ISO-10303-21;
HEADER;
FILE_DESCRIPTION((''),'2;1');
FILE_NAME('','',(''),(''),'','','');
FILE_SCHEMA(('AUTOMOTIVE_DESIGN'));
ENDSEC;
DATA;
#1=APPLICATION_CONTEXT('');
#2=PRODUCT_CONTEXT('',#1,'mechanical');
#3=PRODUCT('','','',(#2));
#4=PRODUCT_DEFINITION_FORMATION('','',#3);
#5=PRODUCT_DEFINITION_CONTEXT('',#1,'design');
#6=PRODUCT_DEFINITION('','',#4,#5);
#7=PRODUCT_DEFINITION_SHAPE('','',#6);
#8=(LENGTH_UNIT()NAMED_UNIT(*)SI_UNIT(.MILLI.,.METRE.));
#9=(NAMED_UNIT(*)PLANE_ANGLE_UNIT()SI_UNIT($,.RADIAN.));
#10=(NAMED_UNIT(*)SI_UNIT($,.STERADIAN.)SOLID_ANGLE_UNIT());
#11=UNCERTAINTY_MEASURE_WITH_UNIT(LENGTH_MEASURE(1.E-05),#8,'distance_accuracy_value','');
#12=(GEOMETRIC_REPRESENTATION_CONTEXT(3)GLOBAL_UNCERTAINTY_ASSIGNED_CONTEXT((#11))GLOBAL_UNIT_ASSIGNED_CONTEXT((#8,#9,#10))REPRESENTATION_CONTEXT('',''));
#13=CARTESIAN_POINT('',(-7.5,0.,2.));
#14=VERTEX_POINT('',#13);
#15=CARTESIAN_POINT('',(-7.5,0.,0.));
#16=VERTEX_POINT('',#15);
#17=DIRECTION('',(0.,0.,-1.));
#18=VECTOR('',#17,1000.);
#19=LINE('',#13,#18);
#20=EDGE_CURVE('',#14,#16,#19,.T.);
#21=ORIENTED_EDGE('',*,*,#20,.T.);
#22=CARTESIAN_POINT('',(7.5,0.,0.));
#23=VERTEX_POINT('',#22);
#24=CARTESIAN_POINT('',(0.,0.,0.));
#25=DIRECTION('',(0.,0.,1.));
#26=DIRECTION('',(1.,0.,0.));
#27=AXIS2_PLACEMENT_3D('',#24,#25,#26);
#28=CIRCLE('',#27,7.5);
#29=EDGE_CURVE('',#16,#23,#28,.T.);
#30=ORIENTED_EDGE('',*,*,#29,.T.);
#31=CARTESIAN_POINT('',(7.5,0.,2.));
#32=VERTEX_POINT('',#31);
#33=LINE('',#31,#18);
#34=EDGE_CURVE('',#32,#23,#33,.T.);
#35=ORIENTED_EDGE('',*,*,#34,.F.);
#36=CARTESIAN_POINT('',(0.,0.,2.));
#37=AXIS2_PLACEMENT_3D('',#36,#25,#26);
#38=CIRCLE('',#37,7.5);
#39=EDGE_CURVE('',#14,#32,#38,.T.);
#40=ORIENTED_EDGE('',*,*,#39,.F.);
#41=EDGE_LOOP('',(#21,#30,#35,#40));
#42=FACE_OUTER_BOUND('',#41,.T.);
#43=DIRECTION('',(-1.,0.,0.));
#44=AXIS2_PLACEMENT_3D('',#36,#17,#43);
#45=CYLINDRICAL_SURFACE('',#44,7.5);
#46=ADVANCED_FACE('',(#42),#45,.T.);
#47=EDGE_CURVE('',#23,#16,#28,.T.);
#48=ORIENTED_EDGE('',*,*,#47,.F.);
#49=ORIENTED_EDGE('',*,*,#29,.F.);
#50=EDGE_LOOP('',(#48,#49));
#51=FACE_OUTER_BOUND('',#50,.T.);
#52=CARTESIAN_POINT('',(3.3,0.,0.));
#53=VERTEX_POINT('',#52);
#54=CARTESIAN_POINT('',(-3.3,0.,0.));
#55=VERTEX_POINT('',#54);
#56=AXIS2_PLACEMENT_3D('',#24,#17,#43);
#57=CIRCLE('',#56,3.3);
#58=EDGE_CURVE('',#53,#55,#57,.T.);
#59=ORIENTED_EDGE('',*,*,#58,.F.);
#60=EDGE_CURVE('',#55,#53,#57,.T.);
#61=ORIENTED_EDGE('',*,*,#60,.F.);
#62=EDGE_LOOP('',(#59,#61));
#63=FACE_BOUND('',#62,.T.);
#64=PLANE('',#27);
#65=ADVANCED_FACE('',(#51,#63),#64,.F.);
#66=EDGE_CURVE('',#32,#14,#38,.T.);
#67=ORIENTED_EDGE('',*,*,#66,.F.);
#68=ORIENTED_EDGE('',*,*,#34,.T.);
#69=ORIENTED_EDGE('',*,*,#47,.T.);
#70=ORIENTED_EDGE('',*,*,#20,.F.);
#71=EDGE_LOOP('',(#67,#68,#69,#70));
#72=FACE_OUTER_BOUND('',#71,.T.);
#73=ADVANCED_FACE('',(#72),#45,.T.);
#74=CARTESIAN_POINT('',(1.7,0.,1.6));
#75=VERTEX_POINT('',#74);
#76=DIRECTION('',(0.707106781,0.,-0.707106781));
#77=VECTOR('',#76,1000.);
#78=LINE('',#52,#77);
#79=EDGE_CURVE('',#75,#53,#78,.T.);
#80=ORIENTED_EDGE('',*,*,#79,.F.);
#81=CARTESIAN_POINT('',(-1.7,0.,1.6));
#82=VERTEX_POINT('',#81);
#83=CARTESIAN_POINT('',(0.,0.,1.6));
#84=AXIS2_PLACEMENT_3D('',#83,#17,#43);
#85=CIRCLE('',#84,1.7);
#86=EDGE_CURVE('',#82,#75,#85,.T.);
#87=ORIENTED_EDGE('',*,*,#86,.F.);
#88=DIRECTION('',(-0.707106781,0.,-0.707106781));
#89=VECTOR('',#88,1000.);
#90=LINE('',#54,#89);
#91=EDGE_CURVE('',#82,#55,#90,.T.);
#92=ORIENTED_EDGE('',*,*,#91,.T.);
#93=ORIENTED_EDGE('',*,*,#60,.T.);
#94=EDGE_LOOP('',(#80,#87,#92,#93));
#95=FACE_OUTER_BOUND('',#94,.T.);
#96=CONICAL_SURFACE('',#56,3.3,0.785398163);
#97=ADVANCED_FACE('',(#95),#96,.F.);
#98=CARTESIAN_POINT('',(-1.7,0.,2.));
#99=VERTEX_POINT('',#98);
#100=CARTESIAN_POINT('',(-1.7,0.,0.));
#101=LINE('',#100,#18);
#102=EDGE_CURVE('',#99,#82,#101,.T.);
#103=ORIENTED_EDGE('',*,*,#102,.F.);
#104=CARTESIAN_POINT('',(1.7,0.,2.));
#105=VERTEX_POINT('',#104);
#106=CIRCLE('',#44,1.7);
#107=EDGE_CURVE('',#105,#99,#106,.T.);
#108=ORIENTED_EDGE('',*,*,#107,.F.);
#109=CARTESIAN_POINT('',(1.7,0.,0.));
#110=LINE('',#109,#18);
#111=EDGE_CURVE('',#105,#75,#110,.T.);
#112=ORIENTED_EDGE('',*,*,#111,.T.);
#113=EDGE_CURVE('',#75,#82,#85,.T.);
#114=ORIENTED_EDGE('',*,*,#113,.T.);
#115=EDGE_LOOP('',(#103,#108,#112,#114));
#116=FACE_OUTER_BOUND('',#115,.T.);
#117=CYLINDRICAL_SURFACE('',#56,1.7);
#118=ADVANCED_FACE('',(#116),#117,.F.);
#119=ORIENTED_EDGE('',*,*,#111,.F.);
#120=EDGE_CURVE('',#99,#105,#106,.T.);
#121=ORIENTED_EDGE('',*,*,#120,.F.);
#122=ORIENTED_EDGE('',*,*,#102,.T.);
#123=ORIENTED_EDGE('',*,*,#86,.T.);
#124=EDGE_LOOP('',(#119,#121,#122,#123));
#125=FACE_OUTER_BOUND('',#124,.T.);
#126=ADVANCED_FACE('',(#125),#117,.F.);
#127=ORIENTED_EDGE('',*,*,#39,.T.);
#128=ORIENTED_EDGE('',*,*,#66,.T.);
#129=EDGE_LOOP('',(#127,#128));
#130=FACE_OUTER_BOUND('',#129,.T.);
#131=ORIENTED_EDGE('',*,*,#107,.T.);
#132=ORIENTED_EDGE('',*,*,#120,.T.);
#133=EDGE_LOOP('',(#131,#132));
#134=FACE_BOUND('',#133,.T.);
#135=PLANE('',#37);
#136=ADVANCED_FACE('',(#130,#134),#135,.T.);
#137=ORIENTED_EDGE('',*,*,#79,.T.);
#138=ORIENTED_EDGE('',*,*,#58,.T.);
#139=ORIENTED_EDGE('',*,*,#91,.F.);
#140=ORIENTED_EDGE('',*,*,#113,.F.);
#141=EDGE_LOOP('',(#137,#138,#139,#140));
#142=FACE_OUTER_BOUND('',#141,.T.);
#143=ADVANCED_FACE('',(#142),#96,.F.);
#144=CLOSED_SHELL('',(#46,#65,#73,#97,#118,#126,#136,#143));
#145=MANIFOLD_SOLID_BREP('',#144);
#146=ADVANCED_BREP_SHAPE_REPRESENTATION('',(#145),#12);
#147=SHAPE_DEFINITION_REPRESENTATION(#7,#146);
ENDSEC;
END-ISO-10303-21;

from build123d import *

# Parameters (mm, degrees)
SKETCH_1_R      = 7.5
SKETCH_1_R_2    = 1
EXTRUDE_1_DEPTH = 2


with BuildPart() as part:
    # 草图1 → 凸台-拉伸1 (new body)
    with BuildSketch(Plane.XY):
        Circle(SKETCH_1_R)
        Circle(SKETCH_1_R_2, mode=Mode.SUBTRACT)
    extrude(amount=EXTRUDE_1_DEPTH)

    # 草图5 → M3 开槽沉头木螺钉的锥形沉头孔1 (revolve, cut)
    with BuildSketch(Plane.YZ):
        Polygon((0, 0), (0, 2), (1.7, 2), (1.7, 1.6), (3.3, 0), align=None)
    revolve(axis=Axis((0, 0, -6.35), (0, 0, 1)), mode=Mode.SUBTRACT)


solid = part.part
